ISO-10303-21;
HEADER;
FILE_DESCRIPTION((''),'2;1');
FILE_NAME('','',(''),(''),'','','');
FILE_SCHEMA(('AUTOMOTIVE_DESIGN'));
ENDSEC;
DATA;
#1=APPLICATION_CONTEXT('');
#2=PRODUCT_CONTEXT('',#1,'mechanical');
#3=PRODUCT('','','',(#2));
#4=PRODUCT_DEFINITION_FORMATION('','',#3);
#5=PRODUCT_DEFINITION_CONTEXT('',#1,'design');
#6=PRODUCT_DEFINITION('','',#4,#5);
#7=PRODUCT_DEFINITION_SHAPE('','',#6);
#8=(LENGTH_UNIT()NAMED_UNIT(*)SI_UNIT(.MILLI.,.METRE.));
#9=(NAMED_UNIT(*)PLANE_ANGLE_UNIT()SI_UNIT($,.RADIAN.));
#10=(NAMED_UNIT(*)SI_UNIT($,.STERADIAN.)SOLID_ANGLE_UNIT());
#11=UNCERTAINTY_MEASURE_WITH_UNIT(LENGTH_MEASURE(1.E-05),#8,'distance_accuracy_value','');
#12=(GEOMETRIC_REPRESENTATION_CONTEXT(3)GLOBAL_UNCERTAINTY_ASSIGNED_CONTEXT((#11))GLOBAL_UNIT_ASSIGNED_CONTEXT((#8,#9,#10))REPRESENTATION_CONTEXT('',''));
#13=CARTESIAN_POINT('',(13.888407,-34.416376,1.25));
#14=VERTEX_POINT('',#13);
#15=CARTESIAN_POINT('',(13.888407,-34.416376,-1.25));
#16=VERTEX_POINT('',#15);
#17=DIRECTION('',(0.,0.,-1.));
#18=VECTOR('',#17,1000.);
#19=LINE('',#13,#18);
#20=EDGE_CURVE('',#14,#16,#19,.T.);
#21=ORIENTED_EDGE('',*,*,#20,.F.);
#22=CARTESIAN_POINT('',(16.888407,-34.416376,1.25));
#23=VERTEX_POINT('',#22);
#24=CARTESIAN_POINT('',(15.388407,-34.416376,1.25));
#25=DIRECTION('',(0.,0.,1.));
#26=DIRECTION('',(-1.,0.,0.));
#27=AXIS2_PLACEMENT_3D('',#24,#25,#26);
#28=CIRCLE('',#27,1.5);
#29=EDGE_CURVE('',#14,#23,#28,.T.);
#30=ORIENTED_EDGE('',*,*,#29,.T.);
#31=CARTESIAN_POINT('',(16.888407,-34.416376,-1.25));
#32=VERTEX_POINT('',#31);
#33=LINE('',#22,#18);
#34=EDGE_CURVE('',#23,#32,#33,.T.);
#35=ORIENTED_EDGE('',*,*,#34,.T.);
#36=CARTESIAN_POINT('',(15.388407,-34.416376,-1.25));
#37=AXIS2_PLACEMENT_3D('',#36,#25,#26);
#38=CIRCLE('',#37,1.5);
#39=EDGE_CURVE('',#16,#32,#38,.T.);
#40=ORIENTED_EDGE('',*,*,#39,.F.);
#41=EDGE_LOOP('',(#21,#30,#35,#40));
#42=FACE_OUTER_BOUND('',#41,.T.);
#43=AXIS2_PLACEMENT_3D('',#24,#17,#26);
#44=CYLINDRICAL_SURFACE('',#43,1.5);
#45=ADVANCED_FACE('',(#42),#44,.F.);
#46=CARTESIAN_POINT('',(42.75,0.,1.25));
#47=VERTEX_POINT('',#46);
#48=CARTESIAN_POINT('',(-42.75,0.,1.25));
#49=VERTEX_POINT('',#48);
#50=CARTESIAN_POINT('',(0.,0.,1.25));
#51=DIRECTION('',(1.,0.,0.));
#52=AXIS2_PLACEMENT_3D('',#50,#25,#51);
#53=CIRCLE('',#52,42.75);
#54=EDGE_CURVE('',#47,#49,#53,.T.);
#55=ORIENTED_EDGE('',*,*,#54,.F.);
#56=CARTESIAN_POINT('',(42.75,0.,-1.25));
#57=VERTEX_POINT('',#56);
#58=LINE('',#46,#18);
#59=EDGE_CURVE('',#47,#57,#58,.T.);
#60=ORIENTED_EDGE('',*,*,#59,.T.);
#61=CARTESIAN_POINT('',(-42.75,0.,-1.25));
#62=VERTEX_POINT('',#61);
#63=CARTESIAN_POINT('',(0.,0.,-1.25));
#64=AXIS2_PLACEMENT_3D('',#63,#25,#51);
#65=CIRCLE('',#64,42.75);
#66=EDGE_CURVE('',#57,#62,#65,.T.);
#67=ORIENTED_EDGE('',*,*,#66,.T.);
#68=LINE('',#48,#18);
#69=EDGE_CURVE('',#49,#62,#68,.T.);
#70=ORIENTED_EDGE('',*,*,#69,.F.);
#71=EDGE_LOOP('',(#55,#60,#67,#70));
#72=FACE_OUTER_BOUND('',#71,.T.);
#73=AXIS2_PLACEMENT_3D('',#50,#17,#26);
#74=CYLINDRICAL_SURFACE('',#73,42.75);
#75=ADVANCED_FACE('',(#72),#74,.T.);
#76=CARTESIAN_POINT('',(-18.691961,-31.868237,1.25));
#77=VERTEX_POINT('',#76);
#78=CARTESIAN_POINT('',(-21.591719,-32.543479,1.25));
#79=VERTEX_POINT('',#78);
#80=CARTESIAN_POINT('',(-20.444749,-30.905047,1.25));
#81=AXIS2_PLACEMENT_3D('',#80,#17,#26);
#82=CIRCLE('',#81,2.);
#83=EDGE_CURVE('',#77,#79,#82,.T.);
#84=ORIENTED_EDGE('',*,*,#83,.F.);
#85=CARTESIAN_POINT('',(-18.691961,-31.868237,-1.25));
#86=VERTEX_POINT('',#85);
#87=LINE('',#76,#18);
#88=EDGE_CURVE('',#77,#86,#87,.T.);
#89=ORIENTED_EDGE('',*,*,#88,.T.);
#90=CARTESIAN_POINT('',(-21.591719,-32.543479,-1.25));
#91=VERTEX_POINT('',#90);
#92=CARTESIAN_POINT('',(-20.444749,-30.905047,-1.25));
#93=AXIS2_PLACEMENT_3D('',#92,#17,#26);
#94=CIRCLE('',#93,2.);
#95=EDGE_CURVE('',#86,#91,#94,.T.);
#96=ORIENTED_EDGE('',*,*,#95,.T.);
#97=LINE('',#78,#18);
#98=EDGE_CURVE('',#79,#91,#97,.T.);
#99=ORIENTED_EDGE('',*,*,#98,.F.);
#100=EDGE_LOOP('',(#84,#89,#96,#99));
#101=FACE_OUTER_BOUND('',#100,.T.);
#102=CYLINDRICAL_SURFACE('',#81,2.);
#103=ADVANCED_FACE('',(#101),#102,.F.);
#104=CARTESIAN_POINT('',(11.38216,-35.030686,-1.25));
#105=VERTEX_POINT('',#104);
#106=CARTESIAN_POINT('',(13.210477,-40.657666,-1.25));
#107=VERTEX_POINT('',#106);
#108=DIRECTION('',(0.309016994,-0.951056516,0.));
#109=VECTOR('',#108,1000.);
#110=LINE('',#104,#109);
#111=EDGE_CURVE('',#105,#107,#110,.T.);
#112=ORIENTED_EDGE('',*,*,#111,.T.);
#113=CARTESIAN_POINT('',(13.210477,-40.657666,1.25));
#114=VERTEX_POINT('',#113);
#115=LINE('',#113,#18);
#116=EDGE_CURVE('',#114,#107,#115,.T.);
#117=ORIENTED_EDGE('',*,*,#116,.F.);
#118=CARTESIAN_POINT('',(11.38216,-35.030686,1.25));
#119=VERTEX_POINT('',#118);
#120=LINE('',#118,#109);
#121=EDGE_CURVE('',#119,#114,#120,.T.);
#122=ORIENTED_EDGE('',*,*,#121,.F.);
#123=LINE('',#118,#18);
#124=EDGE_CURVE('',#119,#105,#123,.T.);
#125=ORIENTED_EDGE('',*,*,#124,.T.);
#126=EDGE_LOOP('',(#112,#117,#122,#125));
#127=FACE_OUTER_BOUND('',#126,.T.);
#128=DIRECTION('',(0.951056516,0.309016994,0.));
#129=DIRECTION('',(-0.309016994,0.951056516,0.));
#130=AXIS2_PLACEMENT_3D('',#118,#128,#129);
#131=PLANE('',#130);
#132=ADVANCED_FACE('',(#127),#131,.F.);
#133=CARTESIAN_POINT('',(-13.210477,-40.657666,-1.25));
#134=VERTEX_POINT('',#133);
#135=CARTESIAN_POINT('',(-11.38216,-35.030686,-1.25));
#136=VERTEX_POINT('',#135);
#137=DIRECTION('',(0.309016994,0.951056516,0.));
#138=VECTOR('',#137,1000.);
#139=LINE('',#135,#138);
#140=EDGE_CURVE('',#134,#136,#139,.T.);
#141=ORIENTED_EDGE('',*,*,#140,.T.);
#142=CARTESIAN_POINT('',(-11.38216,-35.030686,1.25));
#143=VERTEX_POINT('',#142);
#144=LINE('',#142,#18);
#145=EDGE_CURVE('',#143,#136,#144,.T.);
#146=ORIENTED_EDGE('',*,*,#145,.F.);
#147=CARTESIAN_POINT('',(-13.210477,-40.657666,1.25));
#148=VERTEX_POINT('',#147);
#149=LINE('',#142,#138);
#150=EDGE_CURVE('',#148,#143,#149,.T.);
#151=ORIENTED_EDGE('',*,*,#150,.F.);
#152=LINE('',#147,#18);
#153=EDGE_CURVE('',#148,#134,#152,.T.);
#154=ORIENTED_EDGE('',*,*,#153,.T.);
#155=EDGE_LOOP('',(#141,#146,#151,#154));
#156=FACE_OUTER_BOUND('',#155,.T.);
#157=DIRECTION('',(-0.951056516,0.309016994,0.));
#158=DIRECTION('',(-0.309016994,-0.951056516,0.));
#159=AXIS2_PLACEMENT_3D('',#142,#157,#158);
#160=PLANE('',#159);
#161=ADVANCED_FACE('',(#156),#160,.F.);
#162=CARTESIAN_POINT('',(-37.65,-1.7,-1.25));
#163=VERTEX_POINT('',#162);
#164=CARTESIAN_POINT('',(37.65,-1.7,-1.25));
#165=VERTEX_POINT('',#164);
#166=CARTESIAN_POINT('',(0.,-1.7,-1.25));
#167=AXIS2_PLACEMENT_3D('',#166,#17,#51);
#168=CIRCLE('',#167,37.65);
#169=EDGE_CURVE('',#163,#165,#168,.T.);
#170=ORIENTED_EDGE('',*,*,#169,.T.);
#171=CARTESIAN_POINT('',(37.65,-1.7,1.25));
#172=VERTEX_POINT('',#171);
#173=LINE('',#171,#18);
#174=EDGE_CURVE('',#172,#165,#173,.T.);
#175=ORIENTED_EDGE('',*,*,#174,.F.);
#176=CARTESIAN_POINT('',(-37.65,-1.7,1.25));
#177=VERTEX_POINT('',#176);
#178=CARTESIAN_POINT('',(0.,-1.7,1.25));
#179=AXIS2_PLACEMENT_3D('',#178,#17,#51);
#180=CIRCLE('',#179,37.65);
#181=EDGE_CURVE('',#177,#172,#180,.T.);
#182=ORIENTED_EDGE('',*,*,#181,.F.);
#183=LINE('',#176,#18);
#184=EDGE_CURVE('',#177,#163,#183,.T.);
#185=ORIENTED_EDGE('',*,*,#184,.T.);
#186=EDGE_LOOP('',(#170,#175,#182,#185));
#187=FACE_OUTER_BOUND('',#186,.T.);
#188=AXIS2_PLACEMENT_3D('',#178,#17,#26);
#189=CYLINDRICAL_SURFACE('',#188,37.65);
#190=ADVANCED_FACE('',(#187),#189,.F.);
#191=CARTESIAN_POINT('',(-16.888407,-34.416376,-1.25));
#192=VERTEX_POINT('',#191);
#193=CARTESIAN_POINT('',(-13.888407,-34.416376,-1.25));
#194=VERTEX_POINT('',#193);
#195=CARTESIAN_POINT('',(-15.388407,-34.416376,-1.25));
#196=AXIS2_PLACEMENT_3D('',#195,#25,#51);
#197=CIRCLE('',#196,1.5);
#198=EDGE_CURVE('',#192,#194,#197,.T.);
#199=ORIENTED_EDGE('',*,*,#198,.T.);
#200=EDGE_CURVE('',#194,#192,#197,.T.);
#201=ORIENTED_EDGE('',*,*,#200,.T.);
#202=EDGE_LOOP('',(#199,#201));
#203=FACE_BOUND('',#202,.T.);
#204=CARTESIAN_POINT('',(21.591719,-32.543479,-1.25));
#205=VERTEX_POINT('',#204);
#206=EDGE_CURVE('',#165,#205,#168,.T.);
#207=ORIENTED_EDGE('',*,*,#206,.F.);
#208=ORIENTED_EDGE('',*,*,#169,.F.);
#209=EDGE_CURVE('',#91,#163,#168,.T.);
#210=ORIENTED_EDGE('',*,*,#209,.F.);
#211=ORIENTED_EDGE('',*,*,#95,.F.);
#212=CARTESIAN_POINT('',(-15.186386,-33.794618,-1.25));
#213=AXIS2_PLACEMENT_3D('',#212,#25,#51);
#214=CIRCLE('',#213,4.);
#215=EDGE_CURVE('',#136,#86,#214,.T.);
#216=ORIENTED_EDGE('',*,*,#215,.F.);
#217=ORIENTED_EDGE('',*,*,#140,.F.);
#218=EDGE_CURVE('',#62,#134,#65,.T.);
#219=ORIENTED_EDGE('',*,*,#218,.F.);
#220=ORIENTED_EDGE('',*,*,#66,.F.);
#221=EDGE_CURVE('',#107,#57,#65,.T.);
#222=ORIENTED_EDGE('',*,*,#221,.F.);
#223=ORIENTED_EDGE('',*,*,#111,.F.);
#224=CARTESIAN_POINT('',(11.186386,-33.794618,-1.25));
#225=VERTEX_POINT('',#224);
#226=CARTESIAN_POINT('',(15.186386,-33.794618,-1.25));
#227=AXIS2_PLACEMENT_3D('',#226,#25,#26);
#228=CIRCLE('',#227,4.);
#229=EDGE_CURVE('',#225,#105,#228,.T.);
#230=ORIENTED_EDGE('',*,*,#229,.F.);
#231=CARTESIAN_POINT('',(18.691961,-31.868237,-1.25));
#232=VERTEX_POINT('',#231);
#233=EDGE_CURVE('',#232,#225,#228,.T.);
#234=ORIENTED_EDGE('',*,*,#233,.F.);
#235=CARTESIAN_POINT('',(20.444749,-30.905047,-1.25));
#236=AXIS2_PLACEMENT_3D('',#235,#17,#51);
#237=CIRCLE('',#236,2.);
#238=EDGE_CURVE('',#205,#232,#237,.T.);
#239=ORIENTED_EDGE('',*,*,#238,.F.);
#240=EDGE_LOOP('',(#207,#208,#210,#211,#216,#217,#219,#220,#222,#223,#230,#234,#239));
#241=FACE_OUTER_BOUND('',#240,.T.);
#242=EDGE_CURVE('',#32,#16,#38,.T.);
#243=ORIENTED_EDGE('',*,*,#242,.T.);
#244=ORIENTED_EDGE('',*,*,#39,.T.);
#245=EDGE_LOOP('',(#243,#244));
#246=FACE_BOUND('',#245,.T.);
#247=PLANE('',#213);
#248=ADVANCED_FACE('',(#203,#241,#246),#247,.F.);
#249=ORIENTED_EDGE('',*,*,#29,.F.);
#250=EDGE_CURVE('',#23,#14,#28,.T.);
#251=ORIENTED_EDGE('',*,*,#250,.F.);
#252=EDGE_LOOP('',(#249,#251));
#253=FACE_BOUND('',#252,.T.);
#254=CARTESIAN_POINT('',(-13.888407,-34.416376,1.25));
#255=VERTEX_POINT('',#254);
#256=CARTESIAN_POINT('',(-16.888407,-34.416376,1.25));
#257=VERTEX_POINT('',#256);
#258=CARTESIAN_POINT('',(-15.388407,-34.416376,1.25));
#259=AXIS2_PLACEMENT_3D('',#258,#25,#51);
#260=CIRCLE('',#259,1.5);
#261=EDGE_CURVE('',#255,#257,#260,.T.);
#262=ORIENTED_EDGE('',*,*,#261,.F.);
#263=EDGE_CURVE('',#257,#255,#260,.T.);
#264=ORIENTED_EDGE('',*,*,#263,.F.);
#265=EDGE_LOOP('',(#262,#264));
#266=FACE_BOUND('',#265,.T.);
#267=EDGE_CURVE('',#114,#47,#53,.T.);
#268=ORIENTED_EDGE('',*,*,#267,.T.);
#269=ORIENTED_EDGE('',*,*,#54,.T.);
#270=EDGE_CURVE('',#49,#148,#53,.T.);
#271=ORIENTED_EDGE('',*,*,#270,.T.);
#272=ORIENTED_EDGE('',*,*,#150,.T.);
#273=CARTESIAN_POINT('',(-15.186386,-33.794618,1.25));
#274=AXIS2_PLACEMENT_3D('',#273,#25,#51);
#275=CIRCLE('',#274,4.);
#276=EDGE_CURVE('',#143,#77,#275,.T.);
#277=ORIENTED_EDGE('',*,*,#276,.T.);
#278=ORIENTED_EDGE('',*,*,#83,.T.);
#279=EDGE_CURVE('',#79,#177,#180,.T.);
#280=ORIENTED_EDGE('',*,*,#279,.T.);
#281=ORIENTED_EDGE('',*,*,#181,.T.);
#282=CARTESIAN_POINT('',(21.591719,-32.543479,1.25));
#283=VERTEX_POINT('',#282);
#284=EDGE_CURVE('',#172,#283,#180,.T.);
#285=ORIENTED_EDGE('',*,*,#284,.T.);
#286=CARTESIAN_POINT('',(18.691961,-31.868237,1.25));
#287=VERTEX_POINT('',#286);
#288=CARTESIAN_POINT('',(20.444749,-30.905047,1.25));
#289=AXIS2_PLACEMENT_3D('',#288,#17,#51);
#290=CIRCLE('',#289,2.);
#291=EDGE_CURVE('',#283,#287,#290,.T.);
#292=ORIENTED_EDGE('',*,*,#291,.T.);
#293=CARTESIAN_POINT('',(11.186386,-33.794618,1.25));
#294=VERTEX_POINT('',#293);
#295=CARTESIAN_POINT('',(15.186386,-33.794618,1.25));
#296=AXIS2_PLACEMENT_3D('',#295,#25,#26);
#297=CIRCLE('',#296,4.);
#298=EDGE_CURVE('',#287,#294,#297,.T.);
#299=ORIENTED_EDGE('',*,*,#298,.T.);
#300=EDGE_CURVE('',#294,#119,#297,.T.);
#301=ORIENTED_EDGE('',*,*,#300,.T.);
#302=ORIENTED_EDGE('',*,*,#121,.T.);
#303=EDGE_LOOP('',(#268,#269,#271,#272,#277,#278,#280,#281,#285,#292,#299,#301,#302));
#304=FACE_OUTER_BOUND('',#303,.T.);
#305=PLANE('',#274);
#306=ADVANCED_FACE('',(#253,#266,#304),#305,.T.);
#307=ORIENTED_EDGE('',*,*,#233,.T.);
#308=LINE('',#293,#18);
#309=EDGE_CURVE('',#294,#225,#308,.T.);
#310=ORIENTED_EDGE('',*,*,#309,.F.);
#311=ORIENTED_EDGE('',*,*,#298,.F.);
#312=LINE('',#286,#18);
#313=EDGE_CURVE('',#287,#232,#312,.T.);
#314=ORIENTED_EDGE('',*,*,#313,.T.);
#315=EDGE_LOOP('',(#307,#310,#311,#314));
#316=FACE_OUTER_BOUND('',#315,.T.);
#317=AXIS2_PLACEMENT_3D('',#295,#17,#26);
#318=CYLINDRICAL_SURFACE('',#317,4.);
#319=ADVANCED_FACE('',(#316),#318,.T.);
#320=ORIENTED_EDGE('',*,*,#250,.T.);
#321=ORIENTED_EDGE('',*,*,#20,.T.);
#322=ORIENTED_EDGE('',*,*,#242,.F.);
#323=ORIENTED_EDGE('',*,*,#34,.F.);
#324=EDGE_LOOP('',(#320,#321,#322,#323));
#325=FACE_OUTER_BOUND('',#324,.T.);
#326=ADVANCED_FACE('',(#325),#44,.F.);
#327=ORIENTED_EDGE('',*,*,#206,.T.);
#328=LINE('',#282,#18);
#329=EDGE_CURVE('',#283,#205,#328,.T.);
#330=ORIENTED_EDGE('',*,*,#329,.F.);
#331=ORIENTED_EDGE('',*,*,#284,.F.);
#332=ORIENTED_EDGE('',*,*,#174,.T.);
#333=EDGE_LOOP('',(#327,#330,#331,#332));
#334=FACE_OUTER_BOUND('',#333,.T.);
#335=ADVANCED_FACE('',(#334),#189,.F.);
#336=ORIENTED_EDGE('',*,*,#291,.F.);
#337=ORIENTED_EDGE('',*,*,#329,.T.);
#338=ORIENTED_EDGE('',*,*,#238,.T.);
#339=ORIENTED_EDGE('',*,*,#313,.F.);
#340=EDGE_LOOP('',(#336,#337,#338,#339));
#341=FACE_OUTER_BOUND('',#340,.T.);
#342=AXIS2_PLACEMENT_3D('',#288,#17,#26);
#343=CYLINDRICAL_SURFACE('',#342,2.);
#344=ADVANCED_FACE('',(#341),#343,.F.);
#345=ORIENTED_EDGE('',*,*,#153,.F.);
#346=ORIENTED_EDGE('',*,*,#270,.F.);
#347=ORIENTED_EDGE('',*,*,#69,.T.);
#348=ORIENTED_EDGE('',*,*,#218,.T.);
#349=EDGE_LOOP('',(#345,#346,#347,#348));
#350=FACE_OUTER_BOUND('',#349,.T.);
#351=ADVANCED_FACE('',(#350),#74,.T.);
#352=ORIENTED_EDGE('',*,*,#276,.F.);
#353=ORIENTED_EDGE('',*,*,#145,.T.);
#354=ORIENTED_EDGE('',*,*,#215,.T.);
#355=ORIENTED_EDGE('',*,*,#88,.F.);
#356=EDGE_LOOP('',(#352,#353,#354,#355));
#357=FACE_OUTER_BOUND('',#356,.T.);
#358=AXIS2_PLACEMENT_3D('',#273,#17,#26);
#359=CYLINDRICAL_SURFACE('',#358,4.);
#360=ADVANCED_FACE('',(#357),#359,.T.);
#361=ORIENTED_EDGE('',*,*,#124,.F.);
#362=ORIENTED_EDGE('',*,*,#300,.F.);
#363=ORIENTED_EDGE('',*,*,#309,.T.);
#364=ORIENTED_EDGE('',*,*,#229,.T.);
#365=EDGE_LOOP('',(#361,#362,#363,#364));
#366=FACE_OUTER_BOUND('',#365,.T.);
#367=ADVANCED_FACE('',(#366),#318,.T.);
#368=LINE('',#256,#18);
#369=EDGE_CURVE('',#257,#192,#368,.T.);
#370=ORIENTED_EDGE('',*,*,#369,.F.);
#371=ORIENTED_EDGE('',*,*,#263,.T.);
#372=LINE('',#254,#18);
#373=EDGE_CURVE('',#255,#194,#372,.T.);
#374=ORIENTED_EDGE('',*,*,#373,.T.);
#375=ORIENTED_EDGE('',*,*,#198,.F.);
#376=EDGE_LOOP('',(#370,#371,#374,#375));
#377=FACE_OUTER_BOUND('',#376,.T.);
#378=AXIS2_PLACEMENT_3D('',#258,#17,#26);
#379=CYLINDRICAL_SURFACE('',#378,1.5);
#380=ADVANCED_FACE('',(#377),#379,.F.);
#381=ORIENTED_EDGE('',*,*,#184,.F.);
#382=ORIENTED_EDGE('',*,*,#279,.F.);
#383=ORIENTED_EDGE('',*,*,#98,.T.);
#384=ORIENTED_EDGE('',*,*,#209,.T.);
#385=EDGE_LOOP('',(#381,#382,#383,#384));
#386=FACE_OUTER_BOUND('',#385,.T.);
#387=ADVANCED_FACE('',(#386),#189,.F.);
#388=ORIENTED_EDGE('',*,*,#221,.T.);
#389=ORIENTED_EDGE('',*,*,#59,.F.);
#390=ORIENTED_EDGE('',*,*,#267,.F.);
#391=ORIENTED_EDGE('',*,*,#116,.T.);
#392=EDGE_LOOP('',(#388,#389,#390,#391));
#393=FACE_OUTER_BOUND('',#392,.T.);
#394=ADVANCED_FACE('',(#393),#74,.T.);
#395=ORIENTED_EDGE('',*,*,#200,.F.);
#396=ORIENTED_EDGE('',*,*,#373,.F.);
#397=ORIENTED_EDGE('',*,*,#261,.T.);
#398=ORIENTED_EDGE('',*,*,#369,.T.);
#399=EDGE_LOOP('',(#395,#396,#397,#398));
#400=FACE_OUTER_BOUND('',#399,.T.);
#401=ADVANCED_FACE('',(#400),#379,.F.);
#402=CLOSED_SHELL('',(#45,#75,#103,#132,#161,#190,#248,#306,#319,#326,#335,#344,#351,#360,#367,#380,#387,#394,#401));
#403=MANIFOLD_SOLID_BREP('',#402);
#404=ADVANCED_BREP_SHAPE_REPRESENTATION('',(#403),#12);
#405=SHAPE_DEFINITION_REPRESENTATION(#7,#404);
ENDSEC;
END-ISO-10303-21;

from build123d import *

# Parameters (mm, degrees)
EXTRUDE_962_DEPTH      = 1.25
EXTRUDE_962_DEPTH_BACK = 1.25
SKETCH_1_R             = 1.5


with BuildPart() as part:
    # 草图1 → Extrude 962 (new, two sides: drawn at the far end of the back side and taken through both)
    with BuildSketch(Plane.XY.offset(-EXTRUDE_962_DEPTH_BACK)):
        with BuildLine():
            Line((-11.382159751, -35.030685683), (-13.21047651, -40.657666072))
            ThreePointArc((-13.21047651, -40.657666072), (0, 42.75), (13.21047651, -40.657666072))
            Line((13.21047651, -40.657666072), (11.382159751, -35.030685683))
            ThreePointArc((11.382159751, -35.030685683), (13.598126255, -30.12345555), (18.691961025, -31.868237043))
            ThreePointArc((18.691961025, -31.868237043), (19.991161418, -32.852932397), (21.5917191, -32.543478506))
            ThreePointArc((21.5917191, -32.543478506), (0, 35.95), (-21.5917191, -32.543478506))
            ThreePointArc((-21.5917191, -32.543478506), (-19.991161418, -32.852932397), (-18.691961025, -31.868237043))
            ThreePointArc((-18.691961025, -31.868237043), (-13.598126255, -30.12345555), (-11.382159751, -35.030685683))
        make_face()
        with Locations((-15.388407261, -34.416375782)):
            Circle(SKETCH_1_R, mode=Mode.SUBTRACT)
        with Locations(Location((15.388407261, -34.416375782, 0), (0, 0, 180))):
            Circle(SKETCH_1_R, mode=Mode.SUBTRACT)
    extrude(amount=EXTRUDE_962_DEPTH + EXTRUDE_962_DEPTH_BACK)


solid = part.part
